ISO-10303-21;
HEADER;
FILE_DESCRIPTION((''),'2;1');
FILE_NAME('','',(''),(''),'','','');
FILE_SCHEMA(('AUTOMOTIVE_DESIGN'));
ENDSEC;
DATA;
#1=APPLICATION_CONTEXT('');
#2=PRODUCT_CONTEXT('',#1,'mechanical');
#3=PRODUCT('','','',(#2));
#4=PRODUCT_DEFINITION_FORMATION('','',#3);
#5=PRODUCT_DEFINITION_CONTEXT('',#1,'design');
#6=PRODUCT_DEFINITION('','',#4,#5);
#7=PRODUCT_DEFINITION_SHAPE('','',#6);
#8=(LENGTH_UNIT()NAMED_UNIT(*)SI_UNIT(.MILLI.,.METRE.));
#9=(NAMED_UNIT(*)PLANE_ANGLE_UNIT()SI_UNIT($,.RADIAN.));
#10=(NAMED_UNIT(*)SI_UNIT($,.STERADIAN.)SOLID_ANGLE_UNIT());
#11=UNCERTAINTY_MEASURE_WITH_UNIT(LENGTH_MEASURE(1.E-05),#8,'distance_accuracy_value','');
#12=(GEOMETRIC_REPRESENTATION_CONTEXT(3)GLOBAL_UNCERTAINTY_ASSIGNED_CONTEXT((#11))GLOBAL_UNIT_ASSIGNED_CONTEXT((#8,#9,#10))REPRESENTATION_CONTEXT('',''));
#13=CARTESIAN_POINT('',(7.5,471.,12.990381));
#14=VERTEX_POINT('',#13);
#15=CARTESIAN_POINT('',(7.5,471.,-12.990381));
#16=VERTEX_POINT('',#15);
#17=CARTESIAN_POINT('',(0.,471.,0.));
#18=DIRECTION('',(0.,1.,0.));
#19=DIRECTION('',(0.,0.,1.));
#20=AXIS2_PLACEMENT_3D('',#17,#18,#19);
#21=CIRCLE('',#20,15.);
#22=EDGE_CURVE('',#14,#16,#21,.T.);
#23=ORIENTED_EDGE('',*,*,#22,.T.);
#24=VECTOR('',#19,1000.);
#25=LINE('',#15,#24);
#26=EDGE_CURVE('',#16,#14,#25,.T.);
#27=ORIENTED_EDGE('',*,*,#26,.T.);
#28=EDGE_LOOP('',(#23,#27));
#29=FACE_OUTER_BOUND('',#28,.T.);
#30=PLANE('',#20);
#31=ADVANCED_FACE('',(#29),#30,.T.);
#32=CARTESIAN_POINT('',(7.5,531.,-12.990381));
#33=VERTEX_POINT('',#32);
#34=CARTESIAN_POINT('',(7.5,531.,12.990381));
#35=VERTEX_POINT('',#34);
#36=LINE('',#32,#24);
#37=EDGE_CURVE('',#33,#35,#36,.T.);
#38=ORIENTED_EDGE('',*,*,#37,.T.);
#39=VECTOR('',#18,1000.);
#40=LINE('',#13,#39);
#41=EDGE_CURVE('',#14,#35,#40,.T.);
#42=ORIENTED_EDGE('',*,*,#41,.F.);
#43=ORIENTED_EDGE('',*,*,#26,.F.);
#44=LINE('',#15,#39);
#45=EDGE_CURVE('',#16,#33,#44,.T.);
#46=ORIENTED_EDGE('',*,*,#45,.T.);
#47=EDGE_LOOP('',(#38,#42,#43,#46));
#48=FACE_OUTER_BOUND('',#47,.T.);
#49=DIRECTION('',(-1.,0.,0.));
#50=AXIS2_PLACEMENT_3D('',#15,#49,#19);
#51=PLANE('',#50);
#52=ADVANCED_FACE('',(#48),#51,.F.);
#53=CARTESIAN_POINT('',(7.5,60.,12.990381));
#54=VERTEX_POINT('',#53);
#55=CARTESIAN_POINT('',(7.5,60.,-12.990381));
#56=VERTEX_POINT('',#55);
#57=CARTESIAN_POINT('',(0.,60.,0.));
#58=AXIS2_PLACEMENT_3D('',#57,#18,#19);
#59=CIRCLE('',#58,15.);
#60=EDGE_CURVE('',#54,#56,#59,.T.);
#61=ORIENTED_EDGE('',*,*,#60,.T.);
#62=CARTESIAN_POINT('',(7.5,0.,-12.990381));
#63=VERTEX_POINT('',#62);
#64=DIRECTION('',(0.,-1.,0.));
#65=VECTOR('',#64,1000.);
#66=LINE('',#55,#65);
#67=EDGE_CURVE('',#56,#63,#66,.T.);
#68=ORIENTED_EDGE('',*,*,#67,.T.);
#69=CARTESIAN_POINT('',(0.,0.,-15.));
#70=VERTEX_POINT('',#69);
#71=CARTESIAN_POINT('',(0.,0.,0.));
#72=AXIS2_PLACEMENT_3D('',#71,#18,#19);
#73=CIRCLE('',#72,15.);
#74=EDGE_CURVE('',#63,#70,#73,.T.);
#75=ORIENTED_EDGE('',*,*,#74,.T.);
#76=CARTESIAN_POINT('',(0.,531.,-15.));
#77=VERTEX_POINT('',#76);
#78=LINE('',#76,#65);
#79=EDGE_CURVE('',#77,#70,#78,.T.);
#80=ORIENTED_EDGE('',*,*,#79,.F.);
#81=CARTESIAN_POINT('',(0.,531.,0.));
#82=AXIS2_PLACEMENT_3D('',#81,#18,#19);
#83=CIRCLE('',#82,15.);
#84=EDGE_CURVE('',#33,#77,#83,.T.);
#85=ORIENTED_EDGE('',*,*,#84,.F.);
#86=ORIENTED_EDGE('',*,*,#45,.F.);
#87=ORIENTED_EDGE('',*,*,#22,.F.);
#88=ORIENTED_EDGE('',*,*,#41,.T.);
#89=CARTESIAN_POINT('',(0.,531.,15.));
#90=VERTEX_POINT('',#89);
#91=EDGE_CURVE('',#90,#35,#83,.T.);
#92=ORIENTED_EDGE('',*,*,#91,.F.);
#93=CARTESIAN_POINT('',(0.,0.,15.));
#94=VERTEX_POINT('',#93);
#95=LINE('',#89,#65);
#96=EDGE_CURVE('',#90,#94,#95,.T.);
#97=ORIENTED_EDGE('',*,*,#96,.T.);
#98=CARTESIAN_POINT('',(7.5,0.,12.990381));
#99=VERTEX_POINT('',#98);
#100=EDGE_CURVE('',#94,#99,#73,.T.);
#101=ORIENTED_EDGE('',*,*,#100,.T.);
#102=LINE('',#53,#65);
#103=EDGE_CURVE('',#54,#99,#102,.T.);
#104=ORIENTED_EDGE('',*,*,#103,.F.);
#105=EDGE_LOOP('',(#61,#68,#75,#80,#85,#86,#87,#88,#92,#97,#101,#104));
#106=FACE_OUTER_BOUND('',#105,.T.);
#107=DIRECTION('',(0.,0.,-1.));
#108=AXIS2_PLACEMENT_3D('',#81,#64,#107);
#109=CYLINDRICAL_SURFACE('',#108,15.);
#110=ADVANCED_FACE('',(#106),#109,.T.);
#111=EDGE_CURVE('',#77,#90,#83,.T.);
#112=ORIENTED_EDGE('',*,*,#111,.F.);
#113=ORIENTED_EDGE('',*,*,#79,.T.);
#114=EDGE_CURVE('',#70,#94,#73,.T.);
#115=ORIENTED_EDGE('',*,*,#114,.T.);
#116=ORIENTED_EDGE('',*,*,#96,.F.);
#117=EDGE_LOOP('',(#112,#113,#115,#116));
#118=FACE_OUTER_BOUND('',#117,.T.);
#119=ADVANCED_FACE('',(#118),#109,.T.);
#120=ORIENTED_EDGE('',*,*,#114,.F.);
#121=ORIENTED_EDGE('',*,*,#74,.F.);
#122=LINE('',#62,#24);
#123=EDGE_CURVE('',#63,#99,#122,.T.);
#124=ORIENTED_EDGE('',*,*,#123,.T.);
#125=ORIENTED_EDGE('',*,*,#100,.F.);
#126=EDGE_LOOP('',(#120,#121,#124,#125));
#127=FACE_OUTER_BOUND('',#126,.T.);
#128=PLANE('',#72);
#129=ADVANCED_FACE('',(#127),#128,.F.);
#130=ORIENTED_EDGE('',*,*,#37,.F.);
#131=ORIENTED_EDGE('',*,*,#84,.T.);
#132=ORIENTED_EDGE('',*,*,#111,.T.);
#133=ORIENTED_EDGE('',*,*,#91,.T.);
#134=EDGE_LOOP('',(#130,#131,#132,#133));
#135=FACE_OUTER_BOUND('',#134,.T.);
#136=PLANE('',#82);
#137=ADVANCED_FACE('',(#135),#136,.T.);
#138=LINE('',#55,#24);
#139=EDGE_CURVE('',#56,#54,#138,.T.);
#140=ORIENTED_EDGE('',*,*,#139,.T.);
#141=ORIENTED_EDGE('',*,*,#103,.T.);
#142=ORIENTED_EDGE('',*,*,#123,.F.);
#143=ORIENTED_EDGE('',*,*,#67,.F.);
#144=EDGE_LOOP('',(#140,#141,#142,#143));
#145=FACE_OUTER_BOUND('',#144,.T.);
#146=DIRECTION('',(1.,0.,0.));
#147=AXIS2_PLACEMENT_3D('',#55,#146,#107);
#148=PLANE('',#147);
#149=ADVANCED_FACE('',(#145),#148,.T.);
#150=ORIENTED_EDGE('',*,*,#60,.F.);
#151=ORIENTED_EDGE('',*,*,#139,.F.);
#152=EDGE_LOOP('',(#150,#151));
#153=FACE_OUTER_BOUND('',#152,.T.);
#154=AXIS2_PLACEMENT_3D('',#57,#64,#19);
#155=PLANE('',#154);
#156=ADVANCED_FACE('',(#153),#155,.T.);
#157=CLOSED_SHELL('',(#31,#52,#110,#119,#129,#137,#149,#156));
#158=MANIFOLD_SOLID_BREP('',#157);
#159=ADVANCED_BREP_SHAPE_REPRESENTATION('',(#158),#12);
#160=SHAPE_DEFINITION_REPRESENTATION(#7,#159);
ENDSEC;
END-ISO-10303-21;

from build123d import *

# Parameters (mm, degrees)
SKETCH_1_R          = 15
EXTRUDE_1_DEPTH     = 531
CUT_EXTRUDE_START   = -60
CUT_EXTRUDE_1_DEPTH = 60


with BuildPart() as part:
    # 草图1 → 凸台-拉伸1 (new body)
    with BuildSketch(Plane(origin=(0, 0, 0), x_dir=(1, 0, 0), z_dir=(0, 1, 0))):
        with Locations(Location((0, 0, 0), (0, 0, 270))):
            Circle(SKETCH_1_R)
    extrude(amount=EXTRUDE_1_DEPTH)

    # 草图2 → 切除-拉伸1 (cut)
    with BuildSketch(Plane(origin=(0, 531, 0), x_dir=(1, 0, 0), z_dir=(0, 1, 0)).offset(CUT_EXTRUDE_START)):
        with BuildLine():
            Line((7.5, 12.990381057), (7.5, -12.990381057))
            ThreePointArc((7.5, -12.990381057), (15, 0), (7.5, 12.990381057))
        make_face()
    cut_extrude_1 = extrude(amount=CUT_EXTRUDE_1_DEPTH, mode=Mode.SUBTRACT)

    # 镜向1: 切除-拉伸1 across plane
    add(cut_extrude_1.mirror(Plane.ZX.offset(265.5)), mode=Mode.SUBTRACT)


solid = part.part
